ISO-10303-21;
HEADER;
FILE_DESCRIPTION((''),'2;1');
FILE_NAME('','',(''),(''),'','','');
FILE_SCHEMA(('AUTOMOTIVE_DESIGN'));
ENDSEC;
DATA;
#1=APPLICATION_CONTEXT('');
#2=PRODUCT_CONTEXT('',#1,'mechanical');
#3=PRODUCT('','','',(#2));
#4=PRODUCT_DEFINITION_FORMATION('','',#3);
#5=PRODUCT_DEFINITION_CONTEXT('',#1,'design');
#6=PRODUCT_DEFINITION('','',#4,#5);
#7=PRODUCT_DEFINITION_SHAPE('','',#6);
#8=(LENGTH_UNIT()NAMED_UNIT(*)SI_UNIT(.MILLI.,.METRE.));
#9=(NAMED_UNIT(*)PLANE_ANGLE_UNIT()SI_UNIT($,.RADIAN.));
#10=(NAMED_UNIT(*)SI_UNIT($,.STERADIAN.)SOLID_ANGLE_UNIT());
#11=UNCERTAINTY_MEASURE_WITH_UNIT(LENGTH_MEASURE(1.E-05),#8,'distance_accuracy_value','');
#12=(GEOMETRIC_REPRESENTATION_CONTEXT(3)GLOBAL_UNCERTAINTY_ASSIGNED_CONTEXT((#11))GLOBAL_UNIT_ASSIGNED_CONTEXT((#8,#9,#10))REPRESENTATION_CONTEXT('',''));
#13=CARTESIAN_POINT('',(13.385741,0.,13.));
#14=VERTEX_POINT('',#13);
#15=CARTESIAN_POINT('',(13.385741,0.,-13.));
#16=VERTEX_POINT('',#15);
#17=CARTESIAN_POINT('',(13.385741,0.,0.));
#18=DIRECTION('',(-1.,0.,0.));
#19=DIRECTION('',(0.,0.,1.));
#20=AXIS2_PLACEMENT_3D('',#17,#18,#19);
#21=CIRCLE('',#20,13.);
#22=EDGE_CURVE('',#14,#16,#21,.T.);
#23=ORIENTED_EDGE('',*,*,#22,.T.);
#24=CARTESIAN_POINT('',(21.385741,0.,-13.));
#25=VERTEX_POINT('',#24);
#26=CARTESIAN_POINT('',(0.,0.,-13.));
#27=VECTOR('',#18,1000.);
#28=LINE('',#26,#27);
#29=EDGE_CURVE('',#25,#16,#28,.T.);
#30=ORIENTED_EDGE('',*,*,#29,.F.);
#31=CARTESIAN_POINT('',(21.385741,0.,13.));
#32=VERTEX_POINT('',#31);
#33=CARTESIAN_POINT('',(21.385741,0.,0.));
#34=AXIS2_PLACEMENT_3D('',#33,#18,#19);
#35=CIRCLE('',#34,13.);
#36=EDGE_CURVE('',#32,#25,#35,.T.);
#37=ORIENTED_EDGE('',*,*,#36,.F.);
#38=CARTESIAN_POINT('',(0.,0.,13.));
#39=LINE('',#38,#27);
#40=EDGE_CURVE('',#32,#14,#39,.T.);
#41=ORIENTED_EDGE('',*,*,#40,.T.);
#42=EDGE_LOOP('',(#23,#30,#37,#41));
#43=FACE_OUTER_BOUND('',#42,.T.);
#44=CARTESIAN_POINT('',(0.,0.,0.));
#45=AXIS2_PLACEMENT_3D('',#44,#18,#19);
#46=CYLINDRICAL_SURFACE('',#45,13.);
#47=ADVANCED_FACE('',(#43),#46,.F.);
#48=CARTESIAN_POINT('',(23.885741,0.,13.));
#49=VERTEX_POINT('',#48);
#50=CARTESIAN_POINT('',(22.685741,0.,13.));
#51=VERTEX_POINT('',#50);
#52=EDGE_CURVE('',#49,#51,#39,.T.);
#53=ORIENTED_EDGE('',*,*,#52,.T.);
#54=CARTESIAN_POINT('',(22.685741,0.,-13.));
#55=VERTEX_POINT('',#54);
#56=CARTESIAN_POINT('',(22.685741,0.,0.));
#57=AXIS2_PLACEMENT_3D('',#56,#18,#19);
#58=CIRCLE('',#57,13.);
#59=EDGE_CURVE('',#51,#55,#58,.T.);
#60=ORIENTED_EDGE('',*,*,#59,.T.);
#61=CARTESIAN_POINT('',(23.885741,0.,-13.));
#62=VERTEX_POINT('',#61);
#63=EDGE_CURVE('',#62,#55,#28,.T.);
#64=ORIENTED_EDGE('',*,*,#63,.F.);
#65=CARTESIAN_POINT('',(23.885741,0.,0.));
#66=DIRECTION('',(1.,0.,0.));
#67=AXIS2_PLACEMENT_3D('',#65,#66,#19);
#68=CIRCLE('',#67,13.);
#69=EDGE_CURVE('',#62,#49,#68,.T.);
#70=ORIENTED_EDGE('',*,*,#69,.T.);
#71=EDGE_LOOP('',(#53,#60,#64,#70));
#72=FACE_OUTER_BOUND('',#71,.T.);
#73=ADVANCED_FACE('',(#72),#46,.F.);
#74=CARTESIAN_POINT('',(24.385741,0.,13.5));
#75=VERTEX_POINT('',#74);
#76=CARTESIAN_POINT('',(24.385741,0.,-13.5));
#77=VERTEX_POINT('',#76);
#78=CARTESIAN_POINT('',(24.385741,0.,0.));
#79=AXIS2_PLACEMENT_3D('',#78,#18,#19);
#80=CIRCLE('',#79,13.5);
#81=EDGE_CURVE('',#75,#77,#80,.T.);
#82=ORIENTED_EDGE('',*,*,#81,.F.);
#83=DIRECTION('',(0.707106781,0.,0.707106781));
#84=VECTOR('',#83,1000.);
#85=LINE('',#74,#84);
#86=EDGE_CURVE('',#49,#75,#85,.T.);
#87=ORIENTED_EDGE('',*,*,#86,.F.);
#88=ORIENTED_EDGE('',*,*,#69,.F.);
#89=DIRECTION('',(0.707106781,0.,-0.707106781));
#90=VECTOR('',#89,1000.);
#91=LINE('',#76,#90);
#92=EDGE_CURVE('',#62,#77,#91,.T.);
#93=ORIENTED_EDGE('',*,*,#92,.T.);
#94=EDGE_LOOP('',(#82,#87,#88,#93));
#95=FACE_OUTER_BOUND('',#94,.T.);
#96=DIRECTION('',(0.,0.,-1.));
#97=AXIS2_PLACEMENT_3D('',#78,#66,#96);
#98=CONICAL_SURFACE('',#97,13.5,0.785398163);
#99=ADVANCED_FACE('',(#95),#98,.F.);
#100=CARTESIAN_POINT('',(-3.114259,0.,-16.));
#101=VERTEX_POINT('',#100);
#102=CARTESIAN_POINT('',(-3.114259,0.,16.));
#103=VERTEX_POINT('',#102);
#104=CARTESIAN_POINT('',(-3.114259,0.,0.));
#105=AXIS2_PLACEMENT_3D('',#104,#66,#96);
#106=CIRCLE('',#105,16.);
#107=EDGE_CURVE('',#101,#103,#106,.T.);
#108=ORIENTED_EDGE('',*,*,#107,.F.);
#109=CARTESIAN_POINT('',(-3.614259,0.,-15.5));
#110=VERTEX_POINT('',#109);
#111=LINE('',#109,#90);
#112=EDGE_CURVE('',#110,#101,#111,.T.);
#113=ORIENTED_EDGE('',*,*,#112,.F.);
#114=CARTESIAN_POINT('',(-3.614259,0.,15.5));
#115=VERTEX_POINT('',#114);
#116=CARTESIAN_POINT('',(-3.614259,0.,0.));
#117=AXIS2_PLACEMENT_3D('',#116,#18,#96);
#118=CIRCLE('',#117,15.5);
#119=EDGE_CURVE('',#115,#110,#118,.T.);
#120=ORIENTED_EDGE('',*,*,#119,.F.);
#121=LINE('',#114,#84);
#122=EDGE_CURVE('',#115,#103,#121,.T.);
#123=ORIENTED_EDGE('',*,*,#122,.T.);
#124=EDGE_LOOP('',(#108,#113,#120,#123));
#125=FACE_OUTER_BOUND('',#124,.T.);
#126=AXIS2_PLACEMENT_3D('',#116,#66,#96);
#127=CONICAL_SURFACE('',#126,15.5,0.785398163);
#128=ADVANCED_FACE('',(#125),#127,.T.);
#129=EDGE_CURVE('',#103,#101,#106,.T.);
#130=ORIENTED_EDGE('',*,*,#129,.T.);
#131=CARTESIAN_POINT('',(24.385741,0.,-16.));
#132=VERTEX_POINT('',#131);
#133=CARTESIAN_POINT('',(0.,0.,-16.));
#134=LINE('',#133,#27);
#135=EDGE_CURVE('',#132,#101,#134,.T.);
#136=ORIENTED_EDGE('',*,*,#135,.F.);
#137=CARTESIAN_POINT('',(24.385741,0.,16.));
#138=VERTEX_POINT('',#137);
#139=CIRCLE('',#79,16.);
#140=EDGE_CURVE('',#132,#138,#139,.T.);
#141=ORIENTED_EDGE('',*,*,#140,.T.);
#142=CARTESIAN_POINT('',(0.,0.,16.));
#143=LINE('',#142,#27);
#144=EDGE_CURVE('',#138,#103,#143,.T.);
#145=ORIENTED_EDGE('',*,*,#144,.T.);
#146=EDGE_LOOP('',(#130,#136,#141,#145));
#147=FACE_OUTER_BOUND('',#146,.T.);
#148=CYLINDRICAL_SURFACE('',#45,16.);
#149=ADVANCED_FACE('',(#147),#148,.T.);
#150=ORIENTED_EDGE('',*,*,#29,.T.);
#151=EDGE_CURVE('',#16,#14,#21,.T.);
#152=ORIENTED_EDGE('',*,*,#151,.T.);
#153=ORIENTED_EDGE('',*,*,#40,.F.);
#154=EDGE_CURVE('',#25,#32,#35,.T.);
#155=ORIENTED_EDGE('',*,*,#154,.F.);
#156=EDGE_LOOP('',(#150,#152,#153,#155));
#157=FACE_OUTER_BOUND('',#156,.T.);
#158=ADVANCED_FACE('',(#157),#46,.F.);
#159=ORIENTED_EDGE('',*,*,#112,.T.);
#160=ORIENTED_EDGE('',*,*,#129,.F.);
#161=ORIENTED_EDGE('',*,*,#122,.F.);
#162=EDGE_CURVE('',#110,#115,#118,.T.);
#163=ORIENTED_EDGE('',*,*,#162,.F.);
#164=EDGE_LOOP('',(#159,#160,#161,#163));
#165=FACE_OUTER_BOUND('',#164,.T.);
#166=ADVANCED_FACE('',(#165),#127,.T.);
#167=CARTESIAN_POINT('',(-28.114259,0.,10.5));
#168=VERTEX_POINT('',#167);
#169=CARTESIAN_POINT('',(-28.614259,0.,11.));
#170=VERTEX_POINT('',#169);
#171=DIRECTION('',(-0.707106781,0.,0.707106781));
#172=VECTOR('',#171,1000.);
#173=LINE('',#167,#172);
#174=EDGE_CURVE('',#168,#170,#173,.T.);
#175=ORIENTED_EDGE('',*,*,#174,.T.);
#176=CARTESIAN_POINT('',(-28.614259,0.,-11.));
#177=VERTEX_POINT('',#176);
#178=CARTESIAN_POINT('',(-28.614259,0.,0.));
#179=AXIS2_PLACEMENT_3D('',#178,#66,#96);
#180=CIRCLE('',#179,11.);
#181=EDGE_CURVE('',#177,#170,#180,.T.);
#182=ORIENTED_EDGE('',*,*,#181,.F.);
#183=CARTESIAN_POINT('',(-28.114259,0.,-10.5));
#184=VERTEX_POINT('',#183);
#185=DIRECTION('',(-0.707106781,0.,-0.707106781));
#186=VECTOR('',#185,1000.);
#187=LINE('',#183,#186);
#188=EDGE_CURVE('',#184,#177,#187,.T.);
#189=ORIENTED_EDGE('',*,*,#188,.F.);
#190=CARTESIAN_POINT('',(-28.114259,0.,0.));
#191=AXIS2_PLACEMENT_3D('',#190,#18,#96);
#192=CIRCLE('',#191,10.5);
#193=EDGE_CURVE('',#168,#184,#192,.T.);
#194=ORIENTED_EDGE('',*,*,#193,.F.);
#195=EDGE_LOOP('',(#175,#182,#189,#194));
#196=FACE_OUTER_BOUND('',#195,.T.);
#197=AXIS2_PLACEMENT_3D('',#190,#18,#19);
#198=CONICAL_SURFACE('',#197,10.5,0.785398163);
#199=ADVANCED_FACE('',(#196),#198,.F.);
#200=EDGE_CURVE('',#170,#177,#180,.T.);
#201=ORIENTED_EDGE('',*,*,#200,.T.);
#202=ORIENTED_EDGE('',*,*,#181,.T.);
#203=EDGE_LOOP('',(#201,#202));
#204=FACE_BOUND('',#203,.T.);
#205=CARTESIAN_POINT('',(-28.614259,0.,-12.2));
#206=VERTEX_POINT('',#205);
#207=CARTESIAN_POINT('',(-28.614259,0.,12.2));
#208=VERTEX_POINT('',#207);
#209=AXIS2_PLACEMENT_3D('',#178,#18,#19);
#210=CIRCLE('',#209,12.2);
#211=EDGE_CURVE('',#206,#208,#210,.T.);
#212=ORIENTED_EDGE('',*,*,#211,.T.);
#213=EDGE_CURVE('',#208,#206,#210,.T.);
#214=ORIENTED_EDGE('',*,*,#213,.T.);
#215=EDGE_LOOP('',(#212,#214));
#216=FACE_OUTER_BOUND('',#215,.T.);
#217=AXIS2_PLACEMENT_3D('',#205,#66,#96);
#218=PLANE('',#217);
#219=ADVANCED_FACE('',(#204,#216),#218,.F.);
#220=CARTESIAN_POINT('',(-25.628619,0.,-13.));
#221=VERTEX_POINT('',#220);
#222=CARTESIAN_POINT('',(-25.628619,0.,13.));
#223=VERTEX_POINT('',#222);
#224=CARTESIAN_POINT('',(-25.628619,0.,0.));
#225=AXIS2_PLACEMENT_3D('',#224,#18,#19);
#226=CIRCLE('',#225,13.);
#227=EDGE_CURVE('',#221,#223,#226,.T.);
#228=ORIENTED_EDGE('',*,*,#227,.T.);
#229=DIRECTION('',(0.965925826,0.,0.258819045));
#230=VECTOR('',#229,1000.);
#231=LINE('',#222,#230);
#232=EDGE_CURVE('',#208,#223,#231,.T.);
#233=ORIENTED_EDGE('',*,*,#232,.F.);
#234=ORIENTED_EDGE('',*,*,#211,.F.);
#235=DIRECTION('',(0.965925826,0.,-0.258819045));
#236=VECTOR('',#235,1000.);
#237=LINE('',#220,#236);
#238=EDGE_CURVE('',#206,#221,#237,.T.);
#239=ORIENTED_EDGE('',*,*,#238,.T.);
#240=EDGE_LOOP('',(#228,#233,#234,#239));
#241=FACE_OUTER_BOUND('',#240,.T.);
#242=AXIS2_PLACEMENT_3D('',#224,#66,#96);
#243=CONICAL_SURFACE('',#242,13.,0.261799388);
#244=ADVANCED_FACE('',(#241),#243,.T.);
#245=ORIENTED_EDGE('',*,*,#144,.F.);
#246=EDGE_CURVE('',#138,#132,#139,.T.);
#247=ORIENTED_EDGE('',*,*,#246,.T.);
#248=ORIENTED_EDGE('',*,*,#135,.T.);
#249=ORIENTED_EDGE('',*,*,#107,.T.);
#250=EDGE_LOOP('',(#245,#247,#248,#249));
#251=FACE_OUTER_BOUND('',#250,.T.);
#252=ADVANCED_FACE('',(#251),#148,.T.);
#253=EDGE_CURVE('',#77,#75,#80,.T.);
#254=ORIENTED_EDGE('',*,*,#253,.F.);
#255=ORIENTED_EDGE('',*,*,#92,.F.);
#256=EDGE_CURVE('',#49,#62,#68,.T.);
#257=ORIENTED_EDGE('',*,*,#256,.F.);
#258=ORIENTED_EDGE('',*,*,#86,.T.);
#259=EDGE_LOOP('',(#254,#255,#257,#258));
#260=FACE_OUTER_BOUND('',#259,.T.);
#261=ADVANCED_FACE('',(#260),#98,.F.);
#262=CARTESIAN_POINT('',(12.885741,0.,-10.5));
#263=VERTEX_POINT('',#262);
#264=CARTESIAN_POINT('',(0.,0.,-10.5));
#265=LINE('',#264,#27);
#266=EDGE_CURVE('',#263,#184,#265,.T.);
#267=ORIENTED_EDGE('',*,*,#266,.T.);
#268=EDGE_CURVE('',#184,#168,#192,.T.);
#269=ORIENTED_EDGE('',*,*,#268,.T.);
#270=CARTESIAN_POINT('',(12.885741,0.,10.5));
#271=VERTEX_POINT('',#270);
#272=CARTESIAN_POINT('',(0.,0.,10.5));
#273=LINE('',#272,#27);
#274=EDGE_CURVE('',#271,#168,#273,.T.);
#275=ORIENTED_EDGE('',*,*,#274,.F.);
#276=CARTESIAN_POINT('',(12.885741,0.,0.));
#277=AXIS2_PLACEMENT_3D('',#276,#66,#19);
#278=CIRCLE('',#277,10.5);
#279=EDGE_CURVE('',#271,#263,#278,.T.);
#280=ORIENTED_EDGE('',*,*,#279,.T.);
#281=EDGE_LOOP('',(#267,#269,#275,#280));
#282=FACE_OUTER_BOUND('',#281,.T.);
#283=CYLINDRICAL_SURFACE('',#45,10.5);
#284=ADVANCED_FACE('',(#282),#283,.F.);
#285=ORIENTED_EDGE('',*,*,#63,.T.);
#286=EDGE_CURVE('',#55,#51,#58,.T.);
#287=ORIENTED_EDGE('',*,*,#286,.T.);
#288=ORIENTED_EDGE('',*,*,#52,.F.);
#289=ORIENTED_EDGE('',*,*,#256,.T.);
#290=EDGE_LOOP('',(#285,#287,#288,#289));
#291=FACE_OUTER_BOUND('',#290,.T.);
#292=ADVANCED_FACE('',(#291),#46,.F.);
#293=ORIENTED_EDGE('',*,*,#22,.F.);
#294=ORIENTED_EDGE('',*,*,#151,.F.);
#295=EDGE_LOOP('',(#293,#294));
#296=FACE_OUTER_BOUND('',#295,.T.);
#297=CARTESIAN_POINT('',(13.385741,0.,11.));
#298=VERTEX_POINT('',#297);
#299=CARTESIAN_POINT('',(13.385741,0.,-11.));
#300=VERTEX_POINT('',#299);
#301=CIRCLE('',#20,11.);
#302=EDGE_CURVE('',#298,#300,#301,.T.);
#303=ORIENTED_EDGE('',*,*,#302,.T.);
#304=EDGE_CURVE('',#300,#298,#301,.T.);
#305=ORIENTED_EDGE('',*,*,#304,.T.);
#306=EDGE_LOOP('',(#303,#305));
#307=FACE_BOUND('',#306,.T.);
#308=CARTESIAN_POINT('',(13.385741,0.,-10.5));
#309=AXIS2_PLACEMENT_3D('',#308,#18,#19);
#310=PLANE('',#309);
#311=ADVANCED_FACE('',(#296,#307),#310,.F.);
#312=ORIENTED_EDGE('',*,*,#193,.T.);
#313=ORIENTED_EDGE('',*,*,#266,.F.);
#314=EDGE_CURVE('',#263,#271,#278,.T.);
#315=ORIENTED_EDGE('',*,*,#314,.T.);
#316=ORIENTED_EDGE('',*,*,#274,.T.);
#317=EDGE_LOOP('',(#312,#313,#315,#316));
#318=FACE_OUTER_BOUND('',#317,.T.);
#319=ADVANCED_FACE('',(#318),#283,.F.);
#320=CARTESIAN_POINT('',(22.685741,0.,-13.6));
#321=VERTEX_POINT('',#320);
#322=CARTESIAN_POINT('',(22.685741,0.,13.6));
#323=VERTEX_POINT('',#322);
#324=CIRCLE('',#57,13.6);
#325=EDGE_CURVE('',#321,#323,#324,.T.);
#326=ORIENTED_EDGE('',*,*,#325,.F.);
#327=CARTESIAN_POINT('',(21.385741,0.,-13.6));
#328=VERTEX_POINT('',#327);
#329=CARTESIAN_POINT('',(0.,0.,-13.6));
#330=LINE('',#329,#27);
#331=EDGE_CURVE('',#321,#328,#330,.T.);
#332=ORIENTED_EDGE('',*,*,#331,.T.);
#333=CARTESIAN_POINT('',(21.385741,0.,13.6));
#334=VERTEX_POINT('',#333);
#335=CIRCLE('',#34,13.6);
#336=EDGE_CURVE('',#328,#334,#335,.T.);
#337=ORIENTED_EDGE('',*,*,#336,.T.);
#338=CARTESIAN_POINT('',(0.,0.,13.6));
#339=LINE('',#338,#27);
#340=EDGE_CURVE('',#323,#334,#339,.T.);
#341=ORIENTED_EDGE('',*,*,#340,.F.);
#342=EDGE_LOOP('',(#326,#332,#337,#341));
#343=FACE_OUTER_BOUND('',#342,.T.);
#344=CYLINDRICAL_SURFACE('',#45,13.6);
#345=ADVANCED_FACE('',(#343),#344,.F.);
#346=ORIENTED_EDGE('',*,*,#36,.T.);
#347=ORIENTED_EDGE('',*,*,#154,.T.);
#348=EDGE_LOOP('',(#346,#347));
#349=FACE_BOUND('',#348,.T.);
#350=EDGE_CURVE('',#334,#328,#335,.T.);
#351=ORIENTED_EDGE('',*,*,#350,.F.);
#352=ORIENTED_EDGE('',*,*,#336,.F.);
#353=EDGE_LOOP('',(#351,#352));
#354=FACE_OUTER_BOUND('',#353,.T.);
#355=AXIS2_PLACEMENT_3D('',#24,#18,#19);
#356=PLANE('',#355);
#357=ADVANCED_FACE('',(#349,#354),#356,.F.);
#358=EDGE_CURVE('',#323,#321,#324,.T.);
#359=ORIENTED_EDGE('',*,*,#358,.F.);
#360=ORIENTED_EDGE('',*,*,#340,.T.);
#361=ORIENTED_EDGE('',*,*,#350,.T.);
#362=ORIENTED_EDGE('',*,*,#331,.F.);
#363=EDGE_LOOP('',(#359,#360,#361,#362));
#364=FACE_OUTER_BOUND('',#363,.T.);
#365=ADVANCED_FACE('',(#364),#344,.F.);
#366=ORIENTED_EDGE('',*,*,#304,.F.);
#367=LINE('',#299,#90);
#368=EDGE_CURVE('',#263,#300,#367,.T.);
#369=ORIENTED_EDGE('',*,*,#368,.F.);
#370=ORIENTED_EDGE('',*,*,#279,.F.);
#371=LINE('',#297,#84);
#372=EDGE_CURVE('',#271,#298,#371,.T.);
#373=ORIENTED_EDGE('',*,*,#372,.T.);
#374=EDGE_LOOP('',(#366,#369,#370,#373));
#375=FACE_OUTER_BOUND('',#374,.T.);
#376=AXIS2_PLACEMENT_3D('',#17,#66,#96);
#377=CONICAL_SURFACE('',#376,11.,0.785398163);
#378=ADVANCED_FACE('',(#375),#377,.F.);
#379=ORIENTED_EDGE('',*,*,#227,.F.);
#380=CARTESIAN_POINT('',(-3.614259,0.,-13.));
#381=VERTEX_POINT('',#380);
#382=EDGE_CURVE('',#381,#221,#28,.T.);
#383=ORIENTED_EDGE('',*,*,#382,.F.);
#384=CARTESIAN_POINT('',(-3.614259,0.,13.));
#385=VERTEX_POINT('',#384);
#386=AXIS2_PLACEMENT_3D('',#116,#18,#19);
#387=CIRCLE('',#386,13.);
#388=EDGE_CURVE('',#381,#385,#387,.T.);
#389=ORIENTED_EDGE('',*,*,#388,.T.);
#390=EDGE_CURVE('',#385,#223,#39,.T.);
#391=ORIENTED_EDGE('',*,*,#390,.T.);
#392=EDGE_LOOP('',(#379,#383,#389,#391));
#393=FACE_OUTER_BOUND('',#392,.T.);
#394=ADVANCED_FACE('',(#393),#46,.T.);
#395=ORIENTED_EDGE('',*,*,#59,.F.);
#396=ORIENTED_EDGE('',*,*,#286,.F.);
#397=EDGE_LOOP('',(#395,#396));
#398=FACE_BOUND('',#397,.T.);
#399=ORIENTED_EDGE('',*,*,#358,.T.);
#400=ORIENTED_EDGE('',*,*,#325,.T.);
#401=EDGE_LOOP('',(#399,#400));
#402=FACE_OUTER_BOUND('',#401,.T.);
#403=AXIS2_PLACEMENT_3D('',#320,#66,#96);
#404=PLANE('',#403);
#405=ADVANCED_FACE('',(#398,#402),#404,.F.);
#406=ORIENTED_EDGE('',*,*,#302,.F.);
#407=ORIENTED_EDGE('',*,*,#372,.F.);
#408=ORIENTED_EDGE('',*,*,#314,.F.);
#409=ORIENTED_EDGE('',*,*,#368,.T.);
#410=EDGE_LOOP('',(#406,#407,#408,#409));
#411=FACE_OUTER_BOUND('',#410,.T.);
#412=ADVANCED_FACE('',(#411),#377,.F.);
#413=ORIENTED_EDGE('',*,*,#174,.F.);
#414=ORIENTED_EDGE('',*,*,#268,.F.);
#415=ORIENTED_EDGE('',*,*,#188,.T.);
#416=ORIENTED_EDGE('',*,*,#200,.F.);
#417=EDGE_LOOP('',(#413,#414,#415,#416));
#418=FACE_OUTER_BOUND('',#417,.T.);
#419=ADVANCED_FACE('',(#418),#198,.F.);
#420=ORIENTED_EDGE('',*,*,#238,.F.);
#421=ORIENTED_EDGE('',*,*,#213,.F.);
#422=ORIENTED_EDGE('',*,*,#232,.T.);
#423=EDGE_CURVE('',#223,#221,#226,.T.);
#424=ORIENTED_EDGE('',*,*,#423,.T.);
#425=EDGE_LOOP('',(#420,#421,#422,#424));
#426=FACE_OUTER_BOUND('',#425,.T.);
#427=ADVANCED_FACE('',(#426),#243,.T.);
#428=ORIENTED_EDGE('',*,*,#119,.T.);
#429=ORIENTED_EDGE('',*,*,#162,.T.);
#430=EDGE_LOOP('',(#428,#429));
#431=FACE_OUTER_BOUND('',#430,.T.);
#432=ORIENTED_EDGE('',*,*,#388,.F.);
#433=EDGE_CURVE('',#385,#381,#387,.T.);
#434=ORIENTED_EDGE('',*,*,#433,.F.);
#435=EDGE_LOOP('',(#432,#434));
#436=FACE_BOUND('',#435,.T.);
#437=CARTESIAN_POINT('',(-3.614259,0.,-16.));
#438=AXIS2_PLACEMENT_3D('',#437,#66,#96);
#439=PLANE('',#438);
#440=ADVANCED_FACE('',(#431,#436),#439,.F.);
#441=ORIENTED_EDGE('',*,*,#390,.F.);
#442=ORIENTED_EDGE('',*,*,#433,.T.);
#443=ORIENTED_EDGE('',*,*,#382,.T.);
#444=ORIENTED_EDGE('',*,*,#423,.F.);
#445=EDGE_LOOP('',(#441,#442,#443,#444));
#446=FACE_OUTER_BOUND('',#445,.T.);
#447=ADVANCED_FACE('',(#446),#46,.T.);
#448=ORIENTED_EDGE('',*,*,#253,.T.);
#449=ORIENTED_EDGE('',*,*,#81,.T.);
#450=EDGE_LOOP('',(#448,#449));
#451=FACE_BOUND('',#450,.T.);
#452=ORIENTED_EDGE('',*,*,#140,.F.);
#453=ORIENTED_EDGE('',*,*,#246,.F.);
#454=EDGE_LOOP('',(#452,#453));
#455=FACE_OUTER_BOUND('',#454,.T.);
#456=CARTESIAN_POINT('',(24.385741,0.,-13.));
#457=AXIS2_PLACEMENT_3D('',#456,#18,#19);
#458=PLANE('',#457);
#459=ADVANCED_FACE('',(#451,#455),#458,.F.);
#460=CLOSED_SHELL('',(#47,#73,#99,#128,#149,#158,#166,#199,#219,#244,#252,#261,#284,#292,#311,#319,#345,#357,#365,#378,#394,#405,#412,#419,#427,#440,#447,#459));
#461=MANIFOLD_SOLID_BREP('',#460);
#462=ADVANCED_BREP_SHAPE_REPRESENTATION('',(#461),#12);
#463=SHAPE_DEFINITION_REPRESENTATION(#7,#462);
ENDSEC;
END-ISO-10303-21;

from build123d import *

# Parameters (mm, degrees)
CHAMFER_1_SIZE = 0.5


with BuildPart() as part:
    # 草图1 → 旋转1 (revolve)
    with BuildSketch(Plane(origin=(0, 0, 0), x_dir=(1, 0, 0), z_dir=(0, 1, 0)), mode=Mode.PRIVATE) as revolve_1_sk:
        Polygon((-28.614259258, 10.5), (13.385740742, 10.5), (13.385740742, 13), (21.385740742, 13), (21.385740742, 13.6), (22.685740742, 13.6), (22.685740742, 13), (24.385740742, 13), (24.385740742, 16), (-3.614259258, 16), (-3.614259258, 13), (-25.628618612, 13), (-28.614259258, 12.2), align=None)
    revolve(revolve_1_sk.sketch.rotate(Axis((0, 0, 0), (1, 0, 0)), 180), axis=Axis((0, 0, 0), (1, 0, 0)))

    # 倒角1
    chamfer_1_edges = [part.edges().sort_by_distance(p)[0] for p in [
        (-3.614259258, 0, -16),
        (24.385740742, 0, -13),
        (13.385740742, 0, -10.5),
        (-28.614259258, 0, -10.5),
    ]]
    chamfer(chamfer_1_edges, length=CHAMFER_1_SIZE)


solid = part.part
